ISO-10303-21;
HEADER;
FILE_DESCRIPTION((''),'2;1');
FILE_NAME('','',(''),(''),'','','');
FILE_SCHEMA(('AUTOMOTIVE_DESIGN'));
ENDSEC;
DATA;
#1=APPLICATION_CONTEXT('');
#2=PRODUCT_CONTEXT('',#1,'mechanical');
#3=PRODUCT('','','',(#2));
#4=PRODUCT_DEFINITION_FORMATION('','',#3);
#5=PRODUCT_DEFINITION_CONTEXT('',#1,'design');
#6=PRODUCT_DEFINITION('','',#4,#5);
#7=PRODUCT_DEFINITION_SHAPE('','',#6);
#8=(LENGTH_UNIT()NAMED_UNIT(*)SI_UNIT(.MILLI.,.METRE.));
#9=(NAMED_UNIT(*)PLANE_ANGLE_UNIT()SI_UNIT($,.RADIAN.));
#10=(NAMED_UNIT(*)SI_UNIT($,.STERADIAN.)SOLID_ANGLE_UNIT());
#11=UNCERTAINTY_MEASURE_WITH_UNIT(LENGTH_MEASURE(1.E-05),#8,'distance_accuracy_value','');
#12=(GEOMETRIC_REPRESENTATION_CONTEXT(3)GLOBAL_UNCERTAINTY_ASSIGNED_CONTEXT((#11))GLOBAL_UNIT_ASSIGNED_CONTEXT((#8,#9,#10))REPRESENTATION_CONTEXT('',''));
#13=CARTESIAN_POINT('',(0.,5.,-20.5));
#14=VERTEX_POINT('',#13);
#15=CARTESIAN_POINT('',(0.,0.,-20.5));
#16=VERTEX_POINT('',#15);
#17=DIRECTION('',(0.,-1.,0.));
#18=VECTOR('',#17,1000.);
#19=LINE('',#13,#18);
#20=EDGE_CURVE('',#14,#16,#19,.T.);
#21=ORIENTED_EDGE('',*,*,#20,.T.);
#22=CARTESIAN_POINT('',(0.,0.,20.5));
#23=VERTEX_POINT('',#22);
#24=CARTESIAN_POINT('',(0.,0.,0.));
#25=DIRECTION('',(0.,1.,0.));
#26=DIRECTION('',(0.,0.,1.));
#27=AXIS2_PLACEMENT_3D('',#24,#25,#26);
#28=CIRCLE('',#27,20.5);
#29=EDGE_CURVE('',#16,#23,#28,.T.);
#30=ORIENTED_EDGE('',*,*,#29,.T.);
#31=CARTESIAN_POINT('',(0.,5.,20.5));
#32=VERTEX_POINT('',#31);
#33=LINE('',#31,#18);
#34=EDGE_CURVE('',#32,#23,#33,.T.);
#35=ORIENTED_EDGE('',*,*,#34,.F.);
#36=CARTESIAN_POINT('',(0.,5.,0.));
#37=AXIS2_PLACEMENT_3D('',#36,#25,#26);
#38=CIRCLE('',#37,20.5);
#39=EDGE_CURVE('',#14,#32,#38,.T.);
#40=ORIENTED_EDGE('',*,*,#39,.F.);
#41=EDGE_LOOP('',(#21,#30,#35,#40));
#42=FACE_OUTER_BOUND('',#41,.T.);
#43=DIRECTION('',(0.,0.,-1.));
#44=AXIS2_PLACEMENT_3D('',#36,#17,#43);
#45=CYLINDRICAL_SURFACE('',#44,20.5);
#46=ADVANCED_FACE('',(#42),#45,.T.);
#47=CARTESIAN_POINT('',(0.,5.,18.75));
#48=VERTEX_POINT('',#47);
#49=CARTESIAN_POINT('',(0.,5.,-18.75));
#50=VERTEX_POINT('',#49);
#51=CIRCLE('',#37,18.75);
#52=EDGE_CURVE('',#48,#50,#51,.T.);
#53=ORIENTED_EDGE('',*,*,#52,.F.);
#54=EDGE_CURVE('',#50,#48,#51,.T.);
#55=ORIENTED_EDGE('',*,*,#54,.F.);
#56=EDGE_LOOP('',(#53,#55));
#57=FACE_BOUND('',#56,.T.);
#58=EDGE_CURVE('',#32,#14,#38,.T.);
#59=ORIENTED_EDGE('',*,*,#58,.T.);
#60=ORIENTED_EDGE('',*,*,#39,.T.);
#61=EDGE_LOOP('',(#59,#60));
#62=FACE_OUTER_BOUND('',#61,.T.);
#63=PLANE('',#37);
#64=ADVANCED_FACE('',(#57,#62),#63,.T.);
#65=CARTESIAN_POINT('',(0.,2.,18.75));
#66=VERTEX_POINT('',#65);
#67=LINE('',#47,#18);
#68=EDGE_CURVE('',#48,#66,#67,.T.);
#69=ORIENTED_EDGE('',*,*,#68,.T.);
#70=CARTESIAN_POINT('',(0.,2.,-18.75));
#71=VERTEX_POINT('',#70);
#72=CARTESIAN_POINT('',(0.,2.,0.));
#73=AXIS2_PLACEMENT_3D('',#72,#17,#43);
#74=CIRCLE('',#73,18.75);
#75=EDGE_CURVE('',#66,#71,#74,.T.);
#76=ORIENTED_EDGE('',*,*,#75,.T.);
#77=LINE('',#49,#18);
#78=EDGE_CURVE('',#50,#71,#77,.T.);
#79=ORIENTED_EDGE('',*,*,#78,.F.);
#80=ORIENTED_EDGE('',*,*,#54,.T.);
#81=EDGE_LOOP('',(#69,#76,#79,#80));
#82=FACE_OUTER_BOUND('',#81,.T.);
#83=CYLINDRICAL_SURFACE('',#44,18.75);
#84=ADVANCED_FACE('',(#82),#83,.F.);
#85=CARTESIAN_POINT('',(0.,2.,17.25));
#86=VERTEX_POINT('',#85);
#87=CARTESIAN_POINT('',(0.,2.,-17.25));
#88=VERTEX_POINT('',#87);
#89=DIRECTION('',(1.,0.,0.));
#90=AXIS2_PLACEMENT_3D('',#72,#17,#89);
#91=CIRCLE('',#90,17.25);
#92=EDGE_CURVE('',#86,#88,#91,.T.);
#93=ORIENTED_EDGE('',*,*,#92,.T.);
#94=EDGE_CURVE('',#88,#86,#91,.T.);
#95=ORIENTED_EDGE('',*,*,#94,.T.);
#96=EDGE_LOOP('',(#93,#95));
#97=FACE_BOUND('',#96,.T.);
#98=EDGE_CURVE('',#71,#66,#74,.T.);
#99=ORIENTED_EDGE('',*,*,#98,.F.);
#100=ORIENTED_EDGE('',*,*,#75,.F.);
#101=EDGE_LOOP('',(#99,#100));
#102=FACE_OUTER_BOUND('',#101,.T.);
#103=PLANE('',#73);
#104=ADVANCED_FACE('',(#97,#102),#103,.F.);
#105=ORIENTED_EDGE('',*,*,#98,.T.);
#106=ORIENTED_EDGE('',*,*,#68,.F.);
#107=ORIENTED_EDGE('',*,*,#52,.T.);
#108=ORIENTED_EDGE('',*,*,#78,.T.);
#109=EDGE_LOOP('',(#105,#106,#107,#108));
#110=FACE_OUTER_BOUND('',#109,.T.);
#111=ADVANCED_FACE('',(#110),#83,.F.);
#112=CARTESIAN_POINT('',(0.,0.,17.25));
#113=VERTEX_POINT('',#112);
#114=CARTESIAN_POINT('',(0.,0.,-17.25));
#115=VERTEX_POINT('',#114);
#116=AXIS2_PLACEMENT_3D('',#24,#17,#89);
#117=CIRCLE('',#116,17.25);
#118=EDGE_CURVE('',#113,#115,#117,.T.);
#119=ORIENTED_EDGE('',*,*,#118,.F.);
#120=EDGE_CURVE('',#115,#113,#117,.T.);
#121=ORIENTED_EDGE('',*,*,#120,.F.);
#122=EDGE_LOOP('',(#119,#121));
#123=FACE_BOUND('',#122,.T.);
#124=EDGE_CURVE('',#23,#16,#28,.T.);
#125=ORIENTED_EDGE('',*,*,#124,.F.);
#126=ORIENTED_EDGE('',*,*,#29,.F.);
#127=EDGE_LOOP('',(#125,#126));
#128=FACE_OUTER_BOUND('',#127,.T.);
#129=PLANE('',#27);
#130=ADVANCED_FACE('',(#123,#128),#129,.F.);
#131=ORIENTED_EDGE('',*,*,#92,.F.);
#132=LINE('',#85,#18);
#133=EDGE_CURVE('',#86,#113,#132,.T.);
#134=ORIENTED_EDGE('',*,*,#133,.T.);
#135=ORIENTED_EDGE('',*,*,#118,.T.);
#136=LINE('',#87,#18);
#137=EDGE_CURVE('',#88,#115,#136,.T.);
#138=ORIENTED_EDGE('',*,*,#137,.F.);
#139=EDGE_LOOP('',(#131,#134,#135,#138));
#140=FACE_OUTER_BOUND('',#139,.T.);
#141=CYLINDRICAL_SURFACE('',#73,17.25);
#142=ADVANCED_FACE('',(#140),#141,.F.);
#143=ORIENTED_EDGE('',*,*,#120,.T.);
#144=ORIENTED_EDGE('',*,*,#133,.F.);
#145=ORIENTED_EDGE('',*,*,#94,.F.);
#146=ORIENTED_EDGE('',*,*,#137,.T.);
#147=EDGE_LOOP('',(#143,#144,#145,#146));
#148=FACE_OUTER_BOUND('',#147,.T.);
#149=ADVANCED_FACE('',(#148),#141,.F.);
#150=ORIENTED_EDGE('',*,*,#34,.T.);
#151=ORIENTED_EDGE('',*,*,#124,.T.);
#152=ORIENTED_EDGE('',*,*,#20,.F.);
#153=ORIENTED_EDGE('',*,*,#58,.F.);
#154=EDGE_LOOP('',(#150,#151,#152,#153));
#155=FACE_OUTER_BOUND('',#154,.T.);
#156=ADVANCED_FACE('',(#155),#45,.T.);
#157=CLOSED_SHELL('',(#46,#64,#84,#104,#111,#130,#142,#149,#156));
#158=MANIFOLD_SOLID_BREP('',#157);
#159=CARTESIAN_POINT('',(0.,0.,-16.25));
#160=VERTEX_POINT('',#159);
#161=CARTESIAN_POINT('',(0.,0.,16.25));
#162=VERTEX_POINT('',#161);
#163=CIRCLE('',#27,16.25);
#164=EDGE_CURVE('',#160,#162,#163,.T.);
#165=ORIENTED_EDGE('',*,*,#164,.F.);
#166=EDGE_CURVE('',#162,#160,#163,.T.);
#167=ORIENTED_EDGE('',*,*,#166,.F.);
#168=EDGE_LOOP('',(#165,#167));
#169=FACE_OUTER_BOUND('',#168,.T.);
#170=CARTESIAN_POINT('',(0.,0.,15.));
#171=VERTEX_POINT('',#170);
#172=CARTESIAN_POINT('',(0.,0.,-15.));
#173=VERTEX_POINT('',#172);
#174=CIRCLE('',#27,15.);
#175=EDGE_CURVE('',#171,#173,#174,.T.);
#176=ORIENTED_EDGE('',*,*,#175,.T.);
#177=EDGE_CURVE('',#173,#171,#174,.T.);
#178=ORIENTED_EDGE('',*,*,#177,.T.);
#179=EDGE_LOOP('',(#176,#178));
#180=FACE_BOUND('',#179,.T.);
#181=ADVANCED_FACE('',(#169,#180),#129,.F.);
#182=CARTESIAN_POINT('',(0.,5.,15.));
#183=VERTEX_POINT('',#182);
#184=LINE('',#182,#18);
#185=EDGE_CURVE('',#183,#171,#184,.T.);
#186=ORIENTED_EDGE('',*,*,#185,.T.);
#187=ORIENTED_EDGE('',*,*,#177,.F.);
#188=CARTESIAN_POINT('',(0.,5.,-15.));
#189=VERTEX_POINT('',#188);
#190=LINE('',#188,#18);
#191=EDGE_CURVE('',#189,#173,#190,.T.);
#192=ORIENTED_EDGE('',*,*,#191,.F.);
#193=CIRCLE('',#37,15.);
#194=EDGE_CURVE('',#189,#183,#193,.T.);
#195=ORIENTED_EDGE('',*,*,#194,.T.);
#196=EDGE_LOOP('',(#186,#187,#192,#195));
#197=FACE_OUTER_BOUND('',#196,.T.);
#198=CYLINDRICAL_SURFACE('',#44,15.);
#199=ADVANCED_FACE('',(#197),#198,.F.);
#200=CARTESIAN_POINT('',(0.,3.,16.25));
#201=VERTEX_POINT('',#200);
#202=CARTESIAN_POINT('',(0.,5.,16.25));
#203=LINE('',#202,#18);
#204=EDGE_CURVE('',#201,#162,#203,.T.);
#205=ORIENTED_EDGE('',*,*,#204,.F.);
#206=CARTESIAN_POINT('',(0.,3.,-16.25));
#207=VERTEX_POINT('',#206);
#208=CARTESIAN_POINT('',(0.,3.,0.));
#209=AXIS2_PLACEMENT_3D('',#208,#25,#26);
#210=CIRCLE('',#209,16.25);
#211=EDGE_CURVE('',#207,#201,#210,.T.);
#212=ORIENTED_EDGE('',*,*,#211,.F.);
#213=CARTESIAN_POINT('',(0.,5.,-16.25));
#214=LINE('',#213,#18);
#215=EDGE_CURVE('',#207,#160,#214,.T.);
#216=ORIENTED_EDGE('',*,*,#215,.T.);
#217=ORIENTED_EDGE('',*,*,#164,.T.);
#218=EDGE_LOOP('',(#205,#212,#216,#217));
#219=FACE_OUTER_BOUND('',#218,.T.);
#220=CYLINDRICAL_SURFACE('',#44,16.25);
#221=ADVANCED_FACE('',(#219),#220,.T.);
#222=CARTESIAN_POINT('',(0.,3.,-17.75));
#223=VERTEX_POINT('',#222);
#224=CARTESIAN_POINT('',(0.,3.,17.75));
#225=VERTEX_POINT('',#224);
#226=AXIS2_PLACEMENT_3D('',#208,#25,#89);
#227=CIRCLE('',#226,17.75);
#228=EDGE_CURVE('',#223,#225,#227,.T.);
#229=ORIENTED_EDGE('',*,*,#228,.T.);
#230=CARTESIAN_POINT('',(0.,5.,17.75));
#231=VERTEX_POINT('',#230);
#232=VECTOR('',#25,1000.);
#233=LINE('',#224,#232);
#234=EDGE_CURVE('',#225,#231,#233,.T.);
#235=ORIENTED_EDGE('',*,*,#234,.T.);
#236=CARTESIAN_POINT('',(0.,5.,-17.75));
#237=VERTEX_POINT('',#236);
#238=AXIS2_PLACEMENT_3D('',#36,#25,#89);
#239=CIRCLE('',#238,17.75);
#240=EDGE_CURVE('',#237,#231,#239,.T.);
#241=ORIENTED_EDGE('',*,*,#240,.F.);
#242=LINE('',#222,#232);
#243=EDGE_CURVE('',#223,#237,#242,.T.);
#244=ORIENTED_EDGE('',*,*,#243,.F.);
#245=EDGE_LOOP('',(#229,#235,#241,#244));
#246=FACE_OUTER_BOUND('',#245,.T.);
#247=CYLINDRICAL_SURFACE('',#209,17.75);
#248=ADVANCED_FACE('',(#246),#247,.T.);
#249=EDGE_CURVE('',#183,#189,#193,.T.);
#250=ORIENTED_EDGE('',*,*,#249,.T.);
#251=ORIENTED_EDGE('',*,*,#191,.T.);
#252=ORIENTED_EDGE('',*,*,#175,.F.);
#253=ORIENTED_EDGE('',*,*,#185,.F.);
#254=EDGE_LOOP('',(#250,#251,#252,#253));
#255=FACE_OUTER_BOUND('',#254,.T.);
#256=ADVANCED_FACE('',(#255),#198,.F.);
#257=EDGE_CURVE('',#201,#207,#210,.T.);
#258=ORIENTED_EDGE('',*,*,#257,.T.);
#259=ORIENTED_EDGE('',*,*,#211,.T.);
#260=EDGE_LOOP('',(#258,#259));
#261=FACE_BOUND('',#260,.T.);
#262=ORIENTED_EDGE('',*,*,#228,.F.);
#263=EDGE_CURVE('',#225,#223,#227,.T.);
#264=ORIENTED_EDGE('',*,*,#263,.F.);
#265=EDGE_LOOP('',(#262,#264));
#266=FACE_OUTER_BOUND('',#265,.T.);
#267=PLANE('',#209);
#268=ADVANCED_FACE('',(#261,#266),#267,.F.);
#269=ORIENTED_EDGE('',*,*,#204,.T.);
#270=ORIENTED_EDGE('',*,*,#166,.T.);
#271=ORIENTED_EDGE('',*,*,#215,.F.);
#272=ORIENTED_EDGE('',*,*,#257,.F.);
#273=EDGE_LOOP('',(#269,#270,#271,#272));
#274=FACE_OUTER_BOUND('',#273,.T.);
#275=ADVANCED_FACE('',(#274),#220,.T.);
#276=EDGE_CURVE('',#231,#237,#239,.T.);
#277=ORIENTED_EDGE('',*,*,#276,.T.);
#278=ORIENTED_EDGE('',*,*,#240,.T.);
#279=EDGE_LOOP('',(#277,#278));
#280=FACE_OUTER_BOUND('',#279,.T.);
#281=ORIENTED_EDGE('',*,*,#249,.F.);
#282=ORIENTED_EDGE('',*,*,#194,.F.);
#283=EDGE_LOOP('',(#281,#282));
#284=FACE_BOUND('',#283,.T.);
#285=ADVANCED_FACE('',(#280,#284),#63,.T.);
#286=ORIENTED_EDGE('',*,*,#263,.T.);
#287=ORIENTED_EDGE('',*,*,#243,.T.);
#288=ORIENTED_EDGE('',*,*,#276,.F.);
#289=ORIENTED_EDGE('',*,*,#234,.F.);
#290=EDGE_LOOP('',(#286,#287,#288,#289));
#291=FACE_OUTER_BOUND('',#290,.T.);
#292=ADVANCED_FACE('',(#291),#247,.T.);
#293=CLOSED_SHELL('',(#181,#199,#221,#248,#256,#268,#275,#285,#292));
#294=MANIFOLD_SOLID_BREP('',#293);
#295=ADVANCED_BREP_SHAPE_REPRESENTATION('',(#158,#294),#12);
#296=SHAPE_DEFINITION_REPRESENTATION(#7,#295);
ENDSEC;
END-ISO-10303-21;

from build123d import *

# Parameters (mm, degrees)
SKETCH_1_R        = 16.25
SKETCH_1_R_2      = 15
EXTRUDE_1_DEPTH   = 5
SKETCH_1_R_3      = 20.5
SKETCH_1_R_4      = 18.75
EXTRUDE_1_2_DEPTH = 5
EXTRUDE_START     = -2
SKETCH_2_R        = 17.75
SKETCH_2_R_2      = 16.25
EXTRUDE_1_3_DEPTH = 2
SKETCH_3_R        = 18.75
SKETCH_3_R_2      = 17.25
EXTRUDE_2_DEPTH   = 2


with BuildPart() as part:
    # 草图1 → Extrude 1 (new body)
    with BuildSketch(Plane(origin=(0, 0, 0), x_dir=(1, 0, 0), z_dir=(0, 1, 0))):
        with Locations(Location((0, 0, 0), (0, 0, 270))):
            Circle(SKETCH_1_R)
        with Locations(Location((0, 0, 0), (0, 0, 270))):
            Circle(SKETCH_1_R_2, mode=Mode.SUBTRACT)
    extrude(amount=EXTRUDE_1_DEPTH)

    # 草图2 → Extrude 1 3 (add)
    with BuildSketch(Plane(origin=(0, 5, 0), x_dir=(1, 0, 0), z_dir=(0, 1, 0)).offset(EXTRUDE_START)):
        Circle(SKETCH_2_R)
        Circle(SKETCH_2_R_2, mode=Mode.SUBTRACT)
    extrude(amount=EXTRUDE_1_3_DEPTH)


with BuildPart() as body_2:
    # 草图1 → Extrude 1 2 (new body)
    with BuildSketch(Plane(origin=(0, 0, 0), x_dir=(1, 0, 0), z_dir=(0, 1, 0))):
        with Locations(Location((0, 0, 0), (0, 0, 270))):
            Circle(SKETCH_1_R_3)
        with Locations(Location((0, 0, 0), (0, 0, 270))):
            Circle(SKETCH_1_R_4, mode=Mode.SUBTRACT)
    extrude(amount=EXTRUDE_1_2_DEPTH)

    # 草图3 → 拉伸-薄壁2 (add)
    with BuildSketch(Plane.XZ):
        Circle(SKETCH_3_R)
        Circle(SKETCH_3_R_2, mode=Mode.SUBTRACT)
    extrude(amount=-EXTRUDE_2_DEPTH)


solid = Compound([part.part, body_2.part])
